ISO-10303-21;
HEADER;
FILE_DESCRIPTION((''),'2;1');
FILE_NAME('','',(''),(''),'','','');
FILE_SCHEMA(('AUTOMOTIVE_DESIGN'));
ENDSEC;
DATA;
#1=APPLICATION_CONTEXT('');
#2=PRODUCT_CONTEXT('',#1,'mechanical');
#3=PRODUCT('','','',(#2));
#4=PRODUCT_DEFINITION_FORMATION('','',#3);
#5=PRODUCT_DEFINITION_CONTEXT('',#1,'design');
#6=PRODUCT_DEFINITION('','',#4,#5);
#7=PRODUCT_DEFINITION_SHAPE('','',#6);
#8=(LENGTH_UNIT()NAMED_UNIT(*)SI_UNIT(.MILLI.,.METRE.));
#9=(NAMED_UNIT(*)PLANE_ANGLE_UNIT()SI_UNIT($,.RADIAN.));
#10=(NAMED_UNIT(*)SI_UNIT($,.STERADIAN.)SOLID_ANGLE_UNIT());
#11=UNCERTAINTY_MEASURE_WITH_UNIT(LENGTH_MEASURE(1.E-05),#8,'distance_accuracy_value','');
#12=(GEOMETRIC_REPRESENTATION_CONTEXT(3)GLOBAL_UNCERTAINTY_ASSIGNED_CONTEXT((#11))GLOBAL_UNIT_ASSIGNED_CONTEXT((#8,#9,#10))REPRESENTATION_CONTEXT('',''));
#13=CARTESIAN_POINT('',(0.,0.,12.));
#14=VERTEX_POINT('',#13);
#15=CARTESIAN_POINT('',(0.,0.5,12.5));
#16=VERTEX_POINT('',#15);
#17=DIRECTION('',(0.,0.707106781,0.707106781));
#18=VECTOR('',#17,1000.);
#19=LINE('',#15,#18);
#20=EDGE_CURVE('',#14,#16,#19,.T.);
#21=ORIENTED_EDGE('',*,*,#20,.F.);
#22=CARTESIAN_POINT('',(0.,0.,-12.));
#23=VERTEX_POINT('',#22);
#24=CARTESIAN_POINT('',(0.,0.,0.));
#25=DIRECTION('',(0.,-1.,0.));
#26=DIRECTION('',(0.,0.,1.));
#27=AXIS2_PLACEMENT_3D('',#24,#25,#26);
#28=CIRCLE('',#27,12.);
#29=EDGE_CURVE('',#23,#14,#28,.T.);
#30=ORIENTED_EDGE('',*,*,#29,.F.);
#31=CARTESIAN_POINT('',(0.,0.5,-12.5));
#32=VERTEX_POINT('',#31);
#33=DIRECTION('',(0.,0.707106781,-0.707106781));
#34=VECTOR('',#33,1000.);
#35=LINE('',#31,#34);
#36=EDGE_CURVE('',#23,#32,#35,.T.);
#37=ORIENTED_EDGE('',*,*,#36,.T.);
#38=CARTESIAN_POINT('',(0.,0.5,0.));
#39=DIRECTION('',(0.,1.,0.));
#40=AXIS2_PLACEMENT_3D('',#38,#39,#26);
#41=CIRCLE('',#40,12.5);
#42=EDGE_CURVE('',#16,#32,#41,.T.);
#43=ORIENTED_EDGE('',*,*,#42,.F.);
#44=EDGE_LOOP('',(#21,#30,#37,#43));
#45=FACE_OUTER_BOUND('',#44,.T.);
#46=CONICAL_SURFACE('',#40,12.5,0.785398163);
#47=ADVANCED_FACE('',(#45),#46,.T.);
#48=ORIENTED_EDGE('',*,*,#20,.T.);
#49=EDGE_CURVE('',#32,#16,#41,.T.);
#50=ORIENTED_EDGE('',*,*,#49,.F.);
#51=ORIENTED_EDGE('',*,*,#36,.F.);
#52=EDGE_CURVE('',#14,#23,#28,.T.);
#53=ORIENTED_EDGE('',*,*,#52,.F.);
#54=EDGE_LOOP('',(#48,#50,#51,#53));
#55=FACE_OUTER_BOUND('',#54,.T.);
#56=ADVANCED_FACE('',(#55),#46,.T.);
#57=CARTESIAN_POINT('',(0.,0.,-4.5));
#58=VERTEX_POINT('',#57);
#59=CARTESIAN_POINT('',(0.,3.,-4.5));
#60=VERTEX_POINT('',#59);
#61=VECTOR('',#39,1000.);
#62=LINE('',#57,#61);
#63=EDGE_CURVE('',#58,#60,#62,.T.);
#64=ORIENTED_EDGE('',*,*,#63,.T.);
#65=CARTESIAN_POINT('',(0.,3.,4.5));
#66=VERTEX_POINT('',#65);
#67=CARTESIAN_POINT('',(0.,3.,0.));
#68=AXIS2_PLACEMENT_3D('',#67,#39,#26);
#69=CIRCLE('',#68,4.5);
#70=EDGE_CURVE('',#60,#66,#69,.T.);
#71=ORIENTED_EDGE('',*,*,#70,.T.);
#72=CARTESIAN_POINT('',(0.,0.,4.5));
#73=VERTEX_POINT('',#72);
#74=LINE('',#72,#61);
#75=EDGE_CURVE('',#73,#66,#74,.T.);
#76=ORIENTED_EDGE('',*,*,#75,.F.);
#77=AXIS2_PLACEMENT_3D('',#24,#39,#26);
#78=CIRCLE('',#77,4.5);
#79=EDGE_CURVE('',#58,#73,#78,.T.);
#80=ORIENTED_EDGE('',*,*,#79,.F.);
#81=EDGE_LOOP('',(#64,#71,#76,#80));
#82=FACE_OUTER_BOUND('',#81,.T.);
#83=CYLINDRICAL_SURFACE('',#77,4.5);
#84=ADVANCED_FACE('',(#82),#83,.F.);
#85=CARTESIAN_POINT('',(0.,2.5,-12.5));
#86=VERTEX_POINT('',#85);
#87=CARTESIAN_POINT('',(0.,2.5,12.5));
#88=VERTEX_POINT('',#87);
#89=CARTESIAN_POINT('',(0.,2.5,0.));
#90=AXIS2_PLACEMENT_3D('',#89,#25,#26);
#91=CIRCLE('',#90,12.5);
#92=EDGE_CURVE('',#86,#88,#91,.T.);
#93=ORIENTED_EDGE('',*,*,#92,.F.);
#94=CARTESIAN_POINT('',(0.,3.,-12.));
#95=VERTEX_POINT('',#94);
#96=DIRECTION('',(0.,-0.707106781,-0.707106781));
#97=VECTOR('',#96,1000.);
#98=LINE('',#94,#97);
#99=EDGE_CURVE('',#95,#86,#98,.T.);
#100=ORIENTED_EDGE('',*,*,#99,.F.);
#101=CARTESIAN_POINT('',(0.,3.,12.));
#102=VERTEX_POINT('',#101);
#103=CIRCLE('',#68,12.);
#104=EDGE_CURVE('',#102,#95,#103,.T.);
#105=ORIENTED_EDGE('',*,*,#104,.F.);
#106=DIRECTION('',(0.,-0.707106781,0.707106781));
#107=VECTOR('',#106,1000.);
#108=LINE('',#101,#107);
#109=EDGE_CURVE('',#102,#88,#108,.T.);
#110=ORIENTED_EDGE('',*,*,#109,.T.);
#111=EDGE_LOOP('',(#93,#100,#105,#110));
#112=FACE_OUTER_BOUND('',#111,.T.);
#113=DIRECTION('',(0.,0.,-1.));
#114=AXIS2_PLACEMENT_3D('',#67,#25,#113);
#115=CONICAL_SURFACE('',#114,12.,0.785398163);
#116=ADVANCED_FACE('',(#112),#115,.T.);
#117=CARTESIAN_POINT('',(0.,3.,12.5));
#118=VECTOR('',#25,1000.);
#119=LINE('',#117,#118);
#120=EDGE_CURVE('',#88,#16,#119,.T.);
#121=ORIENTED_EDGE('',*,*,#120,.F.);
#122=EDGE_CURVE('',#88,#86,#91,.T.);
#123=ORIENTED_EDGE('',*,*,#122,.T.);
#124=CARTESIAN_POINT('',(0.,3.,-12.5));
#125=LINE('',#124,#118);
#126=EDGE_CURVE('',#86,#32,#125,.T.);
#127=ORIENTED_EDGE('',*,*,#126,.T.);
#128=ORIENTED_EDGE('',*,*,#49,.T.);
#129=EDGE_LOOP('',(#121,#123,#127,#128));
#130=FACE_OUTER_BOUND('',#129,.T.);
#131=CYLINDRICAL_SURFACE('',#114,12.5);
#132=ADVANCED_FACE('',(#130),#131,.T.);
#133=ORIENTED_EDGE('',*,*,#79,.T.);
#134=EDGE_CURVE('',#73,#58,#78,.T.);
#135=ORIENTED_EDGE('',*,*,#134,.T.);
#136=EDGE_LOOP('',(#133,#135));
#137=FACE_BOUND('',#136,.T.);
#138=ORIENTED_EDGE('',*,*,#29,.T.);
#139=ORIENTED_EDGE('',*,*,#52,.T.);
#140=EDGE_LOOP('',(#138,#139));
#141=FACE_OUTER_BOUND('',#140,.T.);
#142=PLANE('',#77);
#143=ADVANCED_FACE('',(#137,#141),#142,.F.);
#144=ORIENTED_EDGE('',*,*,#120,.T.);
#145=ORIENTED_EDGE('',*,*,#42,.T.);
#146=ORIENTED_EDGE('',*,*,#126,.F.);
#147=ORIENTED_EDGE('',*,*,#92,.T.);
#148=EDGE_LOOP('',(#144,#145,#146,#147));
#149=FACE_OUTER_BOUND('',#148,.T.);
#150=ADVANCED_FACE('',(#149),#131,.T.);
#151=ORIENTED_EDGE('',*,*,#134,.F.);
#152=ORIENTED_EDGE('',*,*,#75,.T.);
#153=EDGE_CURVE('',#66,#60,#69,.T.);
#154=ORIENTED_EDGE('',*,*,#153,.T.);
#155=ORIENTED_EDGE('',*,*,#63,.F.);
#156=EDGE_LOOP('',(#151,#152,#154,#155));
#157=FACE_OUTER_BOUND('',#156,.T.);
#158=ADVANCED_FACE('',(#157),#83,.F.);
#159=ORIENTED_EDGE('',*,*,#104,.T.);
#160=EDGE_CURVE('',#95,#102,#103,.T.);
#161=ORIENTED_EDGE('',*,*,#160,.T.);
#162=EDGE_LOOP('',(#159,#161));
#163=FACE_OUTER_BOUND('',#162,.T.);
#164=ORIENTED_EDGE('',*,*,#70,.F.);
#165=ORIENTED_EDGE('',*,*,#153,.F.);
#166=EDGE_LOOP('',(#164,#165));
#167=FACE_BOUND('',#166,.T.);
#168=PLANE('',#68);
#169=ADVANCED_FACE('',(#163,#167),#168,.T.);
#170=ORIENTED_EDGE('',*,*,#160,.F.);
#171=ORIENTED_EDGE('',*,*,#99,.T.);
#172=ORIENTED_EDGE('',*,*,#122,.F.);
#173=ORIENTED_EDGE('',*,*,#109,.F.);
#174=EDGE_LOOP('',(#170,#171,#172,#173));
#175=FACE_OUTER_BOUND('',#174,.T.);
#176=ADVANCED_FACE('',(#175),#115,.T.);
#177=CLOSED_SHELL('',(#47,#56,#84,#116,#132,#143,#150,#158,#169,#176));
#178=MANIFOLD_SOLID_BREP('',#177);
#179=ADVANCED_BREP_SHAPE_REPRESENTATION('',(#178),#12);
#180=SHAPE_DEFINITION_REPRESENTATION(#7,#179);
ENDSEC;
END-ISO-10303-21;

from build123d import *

# Parameters (mm, degrees)
SKETCH_1_R          = 12.5
EXTRUDE_1_DEPTH     = 3
SKETCH_2_R          = 4.5
CUT_EXTRUDE_1_DEPTH = 18.930421077
CHAMFER_1_SIZE      = 0.5


with BuildPart() as part:
    # 草图1 → 凸台-拉伸1 (new body)
    with BuildSketch(Plane(origin=(0, 0, 0), x_dir=(1, 0, 0), z_dir=(0, 1, 0))):
        with Locations(Location((0, 0, 0), (0, 0, 270))):
            Circle(SKETCH_1_R)
    extrude(amount=EXTRUDE_1_DEPTH)

    # 草图2 → 切除-拉伸1 (cut, through all)
    with BuildSketch(Plane(origin=(0, 3, 0), x_dir=(1, 0, 0), z_dir=(0, 1, 0))):
        with Locations(Location((0, 0, 0), (0, 0, 270))):
            Circle(SKETCH_2_R)
    extrude(amount=-CUT_EXTRUDE_1_DEPTH, mode=Mode.SUBTRACT)

    # 倒角1
    chamfer_1_edges = [part.edges().sort_by_distance(p)[0] for p in [
        (0, 0, -12.5),
        (0, 3, -12.5),
    ]]
    chamfer(chamfer_1_edges, length=CHAMFER_1_SIZE)


solid = part.part
